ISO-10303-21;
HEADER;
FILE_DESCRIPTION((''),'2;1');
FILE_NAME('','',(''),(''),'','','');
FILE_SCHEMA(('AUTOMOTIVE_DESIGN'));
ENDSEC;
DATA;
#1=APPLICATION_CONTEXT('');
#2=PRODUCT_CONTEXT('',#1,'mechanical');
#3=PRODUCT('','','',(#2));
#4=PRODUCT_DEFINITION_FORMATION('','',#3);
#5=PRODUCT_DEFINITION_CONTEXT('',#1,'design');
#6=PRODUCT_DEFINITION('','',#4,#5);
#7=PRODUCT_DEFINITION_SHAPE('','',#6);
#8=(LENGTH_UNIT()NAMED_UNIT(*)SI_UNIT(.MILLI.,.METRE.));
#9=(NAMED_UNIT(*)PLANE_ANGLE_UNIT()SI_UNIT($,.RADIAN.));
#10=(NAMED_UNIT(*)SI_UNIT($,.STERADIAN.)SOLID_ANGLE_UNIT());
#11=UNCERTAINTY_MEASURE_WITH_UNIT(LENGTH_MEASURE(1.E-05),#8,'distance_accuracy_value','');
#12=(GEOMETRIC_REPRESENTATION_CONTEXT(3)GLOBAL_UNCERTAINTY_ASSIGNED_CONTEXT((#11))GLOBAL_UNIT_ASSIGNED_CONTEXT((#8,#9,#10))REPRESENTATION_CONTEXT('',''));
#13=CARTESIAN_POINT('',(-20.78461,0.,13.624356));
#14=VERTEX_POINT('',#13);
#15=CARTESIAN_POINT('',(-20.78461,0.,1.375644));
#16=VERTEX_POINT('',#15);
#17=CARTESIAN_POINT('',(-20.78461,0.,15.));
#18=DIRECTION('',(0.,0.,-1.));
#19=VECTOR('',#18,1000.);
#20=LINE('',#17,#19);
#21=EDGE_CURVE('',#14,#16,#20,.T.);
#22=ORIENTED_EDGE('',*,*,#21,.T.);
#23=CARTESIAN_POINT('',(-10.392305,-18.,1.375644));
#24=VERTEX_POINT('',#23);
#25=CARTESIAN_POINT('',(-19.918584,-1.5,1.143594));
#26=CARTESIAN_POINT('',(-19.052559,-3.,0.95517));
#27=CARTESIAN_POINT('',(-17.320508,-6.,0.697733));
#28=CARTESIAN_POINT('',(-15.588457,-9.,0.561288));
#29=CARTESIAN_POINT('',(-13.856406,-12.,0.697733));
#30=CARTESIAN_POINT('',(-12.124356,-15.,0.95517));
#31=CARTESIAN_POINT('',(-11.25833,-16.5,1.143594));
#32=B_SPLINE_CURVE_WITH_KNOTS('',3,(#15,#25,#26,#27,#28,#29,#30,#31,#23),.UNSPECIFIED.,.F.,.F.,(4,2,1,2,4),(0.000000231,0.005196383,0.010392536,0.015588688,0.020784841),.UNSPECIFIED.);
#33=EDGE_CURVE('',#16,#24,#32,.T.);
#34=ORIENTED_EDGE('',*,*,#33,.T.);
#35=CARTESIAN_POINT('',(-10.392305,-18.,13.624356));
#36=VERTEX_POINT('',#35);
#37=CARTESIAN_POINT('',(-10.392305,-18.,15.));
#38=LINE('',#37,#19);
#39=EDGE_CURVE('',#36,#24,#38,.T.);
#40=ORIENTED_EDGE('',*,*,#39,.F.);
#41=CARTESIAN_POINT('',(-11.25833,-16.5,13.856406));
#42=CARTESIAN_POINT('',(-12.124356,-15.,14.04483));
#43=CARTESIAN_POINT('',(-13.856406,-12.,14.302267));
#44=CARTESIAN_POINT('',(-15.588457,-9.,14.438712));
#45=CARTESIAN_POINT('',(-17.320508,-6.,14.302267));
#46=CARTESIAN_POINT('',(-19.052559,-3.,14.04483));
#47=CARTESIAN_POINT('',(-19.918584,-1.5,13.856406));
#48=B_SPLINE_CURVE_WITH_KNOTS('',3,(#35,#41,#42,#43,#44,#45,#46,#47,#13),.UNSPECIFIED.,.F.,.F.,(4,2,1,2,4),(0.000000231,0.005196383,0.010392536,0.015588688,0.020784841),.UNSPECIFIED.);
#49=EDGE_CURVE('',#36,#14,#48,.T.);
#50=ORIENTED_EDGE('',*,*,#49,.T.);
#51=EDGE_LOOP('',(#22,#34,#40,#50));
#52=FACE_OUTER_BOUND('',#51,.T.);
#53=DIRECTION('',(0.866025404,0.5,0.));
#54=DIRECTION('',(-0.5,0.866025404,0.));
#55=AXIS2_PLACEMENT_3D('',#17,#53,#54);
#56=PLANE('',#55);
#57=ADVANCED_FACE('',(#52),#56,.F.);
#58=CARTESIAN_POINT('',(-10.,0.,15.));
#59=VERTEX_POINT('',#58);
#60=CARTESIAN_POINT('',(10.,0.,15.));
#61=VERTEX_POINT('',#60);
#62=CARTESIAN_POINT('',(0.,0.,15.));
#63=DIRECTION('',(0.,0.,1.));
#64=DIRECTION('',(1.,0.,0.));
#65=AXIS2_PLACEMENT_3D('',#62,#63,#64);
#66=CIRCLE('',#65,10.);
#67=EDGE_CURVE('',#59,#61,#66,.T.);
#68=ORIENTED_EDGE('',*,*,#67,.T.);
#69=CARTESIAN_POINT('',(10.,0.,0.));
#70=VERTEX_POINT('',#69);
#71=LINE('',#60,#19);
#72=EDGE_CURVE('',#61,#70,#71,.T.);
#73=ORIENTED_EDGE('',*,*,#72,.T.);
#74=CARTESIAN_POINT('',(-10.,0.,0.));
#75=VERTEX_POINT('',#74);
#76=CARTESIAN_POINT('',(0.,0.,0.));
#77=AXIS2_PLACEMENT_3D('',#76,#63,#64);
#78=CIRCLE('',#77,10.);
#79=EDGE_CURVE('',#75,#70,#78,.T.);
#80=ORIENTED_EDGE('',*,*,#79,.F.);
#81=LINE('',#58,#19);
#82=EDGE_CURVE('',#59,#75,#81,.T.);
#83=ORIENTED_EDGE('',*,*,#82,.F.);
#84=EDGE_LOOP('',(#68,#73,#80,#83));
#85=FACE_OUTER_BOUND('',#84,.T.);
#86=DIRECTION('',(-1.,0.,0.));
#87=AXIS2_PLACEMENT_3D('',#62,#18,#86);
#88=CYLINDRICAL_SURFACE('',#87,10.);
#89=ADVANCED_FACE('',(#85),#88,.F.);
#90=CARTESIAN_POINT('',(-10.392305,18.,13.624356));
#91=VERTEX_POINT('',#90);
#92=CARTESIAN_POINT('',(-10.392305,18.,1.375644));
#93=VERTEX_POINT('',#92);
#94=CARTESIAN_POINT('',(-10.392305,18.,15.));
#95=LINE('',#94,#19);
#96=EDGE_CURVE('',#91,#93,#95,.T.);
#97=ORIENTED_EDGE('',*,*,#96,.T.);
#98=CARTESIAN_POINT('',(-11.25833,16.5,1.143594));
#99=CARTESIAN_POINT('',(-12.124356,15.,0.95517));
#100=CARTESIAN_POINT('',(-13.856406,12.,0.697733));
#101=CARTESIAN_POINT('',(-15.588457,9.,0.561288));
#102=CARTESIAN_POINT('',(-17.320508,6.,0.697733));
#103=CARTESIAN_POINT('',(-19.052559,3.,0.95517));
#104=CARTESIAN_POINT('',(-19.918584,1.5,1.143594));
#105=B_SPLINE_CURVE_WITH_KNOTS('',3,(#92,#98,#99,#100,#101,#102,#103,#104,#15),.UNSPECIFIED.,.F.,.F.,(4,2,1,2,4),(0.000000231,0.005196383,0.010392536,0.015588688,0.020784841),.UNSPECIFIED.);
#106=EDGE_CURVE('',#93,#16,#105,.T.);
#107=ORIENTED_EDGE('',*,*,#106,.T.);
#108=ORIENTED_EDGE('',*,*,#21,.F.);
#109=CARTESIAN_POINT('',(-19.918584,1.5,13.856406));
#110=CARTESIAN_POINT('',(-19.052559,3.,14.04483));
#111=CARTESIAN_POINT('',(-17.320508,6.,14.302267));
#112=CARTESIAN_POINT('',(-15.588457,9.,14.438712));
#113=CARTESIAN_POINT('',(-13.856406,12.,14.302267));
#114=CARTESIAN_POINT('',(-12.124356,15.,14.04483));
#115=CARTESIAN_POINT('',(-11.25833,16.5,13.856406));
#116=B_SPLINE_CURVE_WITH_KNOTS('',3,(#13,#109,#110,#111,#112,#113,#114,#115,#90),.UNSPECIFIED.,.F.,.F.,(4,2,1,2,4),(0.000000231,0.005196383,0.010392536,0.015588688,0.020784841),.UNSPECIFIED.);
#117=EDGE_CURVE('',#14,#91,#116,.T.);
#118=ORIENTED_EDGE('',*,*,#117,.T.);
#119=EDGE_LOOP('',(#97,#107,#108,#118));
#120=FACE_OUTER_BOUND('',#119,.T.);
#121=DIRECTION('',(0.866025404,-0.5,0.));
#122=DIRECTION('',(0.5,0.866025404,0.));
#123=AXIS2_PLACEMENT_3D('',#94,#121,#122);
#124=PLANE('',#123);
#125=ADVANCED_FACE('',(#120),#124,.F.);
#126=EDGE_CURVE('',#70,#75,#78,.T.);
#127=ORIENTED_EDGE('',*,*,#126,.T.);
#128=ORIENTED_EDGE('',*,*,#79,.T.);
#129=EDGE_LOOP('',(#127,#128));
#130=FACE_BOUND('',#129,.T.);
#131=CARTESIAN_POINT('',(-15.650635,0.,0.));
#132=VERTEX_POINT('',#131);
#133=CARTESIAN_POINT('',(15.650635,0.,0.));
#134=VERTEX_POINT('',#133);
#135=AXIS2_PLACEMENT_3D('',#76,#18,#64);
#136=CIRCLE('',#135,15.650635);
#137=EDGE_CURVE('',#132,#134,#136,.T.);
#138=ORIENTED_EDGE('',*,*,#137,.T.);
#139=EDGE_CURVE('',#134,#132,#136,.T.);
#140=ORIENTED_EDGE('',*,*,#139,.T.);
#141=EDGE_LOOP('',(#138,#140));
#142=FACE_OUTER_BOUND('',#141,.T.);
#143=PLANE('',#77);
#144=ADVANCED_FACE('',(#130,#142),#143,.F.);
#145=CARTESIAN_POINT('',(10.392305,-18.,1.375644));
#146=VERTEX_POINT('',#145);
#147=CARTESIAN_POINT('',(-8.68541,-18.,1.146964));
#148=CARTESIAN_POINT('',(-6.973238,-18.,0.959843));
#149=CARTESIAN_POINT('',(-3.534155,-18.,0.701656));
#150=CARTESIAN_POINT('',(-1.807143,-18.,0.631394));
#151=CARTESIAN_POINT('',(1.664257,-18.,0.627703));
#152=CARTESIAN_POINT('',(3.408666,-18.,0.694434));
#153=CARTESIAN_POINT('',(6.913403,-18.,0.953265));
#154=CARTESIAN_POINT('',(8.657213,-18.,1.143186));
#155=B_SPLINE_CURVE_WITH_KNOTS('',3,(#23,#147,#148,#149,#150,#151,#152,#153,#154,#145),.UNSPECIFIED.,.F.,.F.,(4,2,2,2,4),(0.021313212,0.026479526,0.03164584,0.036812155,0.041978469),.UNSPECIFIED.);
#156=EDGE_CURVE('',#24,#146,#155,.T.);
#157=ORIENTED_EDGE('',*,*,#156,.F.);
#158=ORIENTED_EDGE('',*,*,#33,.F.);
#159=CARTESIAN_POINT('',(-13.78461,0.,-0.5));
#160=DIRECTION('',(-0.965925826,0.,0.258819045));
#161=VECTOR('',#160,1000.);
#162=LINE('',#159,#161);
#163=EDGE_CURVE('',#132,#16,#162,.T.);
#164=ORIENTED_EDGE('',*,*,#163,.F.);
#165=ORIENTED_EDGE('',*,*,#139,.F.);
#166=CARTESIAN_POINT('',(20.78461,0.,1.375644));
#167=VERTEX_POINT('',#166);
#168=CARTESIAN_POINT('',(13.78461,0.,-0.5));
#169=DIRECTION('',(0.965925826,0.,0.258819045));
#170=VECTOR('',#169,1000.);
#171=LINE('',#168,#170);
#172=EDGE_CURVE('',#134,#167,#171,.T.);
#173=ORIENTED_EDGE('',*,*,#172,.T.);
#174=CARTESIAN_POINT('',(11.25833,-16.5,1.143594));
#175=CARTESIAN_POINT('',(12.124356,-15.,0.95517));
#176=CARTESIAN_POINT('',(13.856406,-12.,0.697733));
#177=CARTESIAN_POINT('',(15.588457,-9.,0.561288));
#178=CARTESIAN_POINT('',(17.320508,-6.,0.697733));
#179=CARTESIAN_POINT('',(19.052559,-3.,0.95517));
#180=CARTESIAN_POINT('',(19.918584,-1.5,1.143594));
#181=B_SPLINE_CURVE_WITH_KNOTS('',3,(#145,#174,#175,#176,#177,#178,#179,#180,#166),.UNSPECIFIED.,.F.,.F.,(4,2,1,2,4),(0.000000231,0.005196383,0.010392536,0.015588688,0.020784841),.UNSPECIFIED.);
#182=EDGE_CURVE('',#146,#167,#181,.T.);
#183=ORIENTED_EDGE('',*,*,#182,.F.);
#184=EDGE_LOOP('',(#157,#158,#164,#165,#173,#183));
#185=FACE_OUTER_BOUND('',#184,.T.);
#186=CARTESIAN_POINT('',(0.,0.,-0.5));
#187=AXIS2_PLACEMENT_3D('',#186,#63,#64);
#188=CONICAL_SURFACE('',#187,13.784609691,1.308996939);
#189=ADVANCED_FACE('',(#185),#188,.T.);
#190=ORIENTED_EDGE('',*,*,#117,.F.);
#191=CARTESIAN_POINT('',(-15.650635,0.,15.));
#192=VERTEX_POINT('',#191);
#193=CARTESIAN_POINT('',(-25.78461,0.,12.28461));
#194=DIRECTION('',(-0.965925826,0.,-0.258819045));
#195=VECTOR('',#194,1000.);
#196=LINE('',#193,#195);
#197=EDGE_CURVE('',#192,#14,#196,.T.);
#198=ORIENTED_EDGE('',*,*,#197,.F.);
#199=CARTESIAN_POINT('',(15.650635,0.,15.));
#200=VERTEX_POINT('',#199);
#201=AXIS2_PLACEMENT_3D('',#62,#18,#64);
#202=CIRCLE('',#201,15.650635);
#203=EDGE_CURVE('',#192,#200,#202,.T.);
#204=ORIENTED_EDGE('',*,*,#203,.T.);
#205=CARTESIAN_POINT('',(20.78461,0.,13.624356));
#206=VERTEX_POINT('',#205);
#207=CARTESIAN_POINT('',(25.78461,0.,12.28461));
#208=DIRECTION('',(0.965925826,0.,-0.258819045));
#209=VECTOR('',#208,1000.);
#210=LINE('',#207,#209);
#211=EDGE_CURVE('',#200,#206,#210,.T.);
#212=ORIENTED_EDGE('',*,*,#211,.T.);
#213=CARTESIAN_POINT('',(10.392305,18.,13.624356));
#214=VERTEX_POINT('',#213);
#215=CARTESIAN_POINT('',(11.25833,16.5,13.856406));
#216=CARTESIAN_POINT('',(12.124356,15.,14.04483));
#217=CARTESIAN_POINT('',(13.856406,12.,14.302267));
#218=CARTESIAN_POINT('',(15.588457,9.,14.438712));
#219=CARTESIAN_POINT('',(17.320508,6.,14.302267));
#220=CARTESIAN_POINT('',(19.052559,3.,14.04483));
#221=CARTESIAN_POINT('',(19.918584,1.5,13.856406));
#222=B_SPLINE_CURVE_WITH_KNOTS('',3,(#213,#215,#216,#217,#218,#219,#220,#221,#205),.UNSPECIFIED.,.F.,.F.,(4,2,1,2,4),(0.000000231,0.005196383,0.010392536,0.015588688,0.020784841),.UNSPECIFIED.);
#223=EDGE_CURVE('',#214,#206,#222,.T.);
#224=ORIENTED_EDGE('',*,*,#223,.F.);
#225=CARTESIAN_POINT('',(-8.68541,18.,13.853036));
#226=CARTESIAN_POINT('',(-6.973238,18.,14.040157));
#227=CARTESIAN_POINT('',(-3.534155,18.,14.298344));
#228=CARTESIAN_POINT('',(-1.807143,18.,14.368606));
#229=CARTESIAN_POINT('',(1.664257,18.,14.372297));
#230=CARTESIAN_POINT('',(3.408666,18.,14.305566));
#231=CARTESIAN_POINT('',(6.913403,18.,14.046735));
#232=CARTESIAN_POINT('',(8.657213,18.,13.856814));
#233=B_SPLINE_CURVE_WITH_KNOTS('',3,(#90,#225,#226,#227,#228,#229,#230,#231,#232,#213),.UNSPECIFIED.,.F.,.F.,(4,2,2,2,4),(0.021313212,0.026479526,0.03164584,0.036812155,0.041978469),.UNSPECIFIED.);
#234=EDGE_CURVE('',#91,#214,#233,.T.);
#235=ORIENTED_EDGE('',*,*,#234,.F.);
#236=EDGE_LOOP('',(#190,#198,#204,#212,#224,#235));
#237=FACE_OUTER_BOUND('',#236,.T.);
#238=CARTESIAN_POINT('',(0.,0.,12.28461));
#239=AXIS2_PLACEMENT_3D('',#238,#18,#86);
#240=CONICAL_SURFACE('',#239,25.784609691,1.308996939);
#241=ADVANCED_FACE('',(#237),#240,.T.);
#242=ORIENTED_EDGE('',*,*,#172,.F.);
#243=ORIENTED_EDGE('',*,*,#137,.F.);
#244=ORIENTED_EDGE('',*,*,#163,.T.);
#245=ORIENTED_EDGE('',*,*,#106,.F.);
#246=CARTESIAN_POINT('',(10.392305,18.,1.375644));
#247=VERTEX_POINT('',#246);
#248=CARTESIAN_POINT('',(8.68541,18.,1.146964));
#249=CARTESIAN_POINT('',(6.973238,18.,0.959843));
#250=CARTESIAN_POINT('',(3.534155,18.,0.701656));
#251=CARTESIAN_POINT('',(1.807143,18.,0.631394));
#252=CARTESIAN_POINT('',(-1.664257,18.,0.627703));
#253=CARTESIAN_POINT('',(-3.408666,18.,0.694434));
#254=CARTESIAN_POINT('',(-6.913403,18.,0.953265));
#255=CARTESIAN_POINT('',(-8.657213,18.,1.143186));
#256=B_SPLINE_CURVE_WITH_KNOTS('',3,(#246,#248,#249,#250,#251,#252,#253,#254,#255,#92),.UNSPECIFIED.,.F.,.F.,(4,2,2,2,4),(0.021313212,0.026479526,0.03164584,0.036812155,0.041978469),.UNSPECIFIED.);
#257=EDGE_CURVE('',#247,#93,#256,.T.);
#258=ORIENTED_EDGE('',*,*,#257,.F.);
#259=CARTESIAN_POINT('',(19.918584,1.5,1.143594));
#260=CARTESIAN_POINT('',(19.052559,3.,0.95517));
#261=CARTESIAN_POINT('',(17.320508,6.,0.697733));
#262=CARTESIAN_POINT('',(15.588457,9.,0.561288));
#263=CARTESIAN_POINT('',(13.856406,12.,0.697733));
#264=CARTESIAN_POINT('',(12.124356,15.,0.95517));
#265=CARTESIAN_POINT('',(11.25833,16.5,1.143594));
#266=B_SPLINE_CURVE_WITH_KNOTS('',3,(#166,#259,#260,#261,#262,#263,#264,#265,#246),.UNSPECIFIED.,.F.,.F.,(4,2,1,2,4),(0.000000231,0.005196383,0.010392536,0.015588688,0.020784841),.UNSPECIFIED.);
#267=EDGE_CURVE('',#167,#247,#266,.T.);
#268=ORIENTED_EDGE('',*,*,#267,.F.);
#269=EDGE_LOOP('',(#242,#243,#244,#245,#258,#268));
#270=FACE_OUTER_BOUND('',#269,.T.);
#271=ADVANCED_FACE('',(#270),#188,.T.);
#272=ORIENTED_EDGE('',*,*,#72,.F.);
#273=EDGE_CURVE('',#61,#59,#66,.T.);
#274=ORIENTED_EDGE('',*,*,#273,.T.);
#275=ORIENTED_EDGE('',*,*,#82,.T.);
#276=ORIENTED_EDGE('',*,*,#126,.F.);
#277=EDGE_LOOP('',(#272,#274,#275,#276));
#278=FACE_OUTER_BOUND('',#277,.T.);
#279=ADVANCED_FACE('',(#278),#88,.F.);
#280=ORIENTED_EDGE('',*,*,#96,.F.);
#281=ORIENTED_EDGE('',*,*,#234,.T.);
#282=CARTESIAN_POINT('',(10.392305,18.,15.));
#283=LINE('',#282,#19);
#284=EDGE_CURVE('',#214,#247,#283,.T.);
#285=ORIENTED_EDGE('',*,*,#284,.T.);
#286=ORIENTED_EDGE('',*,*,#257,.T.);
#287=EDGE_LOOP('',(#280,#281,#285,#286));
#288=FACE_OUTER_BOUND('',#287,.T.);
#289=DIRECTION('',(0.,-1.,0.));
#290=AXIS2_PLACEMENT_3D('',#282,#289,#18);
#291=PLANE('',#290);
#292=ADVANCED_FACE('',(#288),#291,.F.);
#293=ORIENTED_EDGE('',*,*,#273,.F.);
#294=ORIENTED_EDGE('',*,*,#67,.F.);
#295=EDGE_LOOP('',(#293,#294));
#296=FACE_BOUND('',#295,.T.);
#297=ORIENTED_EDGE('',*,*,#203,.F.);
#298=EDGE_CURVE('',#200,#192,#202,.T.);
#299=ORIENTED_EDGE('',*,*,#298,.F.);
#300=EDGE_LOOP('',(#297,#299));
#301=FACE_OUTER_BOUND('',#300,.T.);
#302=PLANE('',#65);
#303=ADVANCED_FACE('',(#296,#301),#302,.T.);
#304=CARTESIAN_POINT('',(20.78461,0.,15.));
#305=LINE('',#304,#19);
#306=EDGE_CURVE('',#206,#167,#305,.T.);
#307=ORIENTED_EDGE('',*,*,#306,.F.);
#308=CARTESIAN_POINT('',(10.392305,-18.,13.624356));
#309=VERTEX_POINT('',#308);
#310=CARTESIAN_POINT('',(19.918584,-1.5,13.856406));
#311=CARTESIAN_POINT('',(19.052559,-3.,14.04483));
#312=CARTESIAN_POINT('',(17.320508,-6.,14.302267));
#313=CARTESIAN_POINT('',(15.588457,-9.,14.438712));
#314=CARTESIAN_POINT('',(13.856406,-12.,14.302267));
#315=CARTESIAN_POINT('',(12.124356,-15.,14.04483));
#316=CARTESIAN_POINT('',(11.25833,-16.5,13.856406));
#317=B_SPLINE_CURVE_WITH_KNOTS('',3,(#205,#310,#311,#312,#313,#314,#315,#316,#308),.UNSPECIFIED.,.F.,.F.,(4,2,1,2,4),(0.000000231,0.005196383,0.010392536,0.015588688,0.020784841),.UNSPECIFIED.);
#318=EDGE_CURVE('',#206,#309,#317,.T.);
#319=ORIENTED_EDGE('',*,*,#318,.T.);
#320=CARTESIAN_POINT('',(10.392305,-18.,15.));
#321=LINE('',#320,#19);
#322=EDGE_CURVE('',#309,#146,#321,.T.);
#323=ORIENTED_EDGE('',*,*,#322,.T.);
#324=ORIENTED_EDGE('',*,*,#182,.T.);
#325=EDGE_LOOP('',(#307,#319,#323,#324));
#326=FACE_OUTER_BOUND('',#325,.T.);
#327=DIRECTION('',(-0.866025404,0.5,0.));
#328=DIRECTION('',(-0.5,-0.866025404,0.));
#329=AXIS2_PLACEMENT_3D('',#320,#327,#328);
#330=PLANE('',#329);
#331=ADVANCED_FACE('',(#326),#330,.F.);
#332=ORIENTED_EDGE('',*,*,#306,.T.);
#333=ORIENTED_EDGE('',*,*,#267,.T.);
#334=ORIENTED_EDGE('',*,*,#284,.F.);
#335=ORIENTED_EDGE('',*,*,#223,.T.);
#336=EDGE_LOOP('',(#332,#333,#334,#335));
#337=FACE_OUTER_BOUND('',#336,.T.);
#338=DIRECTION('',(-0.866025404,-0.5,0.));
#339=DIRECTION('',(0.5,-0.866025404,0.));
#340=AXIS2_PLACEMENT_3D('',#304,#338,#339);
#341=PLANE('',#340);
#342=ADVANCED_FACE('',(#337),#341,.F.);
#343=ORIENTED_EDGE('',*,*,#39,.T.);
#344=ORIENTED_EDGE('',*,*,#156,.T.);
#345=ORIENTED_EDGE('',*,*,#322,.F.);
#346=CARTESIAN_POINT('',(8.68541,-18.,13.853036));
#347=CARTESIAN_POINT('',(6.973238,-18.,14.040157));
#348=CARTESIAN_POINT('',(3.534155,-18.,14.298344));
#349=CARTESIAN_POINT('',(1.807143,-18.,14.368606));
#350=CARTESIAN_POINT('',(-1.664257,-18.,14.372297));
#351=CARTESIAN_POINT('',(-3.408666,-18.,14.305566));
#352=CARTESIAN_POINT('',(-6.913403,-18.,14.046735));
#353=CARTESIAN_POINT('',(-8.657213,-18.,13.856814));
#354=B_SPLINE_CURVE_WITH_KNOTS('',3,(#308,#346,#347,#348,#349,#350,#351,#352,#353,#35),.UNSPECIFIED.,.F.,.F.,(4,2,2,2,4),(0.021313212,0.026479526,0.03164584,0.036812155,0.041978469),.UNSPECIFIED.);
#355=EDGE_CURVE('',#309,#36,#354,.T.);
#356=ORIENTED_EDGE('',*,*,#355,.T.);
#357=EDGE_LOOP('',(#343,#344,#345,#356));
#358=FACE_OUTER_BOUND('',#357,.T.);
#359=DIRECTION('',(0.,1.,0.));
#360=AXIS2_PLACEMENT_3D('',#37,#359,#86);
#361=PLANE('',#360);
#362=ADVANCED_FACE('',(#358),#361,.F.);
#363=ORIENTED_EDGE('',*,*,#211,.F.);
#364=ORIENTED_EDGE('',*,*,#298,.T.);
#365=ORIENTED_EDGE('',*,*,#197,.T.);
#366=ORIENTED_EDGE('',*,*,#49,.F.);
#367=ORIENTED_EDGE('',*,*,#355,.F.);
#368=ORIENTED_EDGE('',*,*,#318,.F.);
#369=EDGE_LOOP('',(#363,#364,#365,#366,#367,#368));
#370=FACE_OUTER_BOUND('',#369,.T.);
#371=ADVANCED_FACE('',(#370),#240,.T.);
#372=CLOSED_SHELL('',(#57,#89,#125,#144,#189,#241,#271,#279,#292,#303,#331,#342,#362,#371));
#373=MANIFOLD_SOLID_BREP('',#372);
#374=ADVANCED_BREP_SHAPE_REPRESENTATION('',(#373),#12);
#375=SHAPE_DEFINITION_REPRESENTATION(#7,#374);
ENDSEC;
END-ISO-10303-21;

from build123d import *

# Parameters (mm, degrees)
SKETCH1_R           = 10
BOSS_EXTRUDE1_DEPTH = 15


with BuildPart() as part:
    # Sketch1 → Boss-Extrude1 (new body)
    with BuildSketch(Plane.XY):
        Polygon((-20.784609691, 0), (-10.392304845, -18), (10.392304845, -18), (20.784609691, 0), (10.392304845, 18), (-10.392304845, 18), align=None)
        Circle(SKETCH1_R, mode=Mode.SUBTRACT)
    extrude(amount=BOSS_EXTRUDE1_DEPTH)

    # Sketch2 → Cut-Revolve1 (revolve, cut)
    with BuildSketch(Plane(origin=(0, 0, 0), x_dir=(1, 0, 0), z_dir=(0, 1, 0))):
        Polygon((13.784609691, 0.5), (25.784609691, -2.715390309), (25.784609691, 0.5), align=None)
        Polygon((25.784609691, -15.5), (25.784609691, -12.284609691), (13.784609691, -15.5), align=None)
    revolve(axis=Axis((0, 0, 15), (0, 0, -1)), mode=Mode.SUBTRACT)


solid = part.part
